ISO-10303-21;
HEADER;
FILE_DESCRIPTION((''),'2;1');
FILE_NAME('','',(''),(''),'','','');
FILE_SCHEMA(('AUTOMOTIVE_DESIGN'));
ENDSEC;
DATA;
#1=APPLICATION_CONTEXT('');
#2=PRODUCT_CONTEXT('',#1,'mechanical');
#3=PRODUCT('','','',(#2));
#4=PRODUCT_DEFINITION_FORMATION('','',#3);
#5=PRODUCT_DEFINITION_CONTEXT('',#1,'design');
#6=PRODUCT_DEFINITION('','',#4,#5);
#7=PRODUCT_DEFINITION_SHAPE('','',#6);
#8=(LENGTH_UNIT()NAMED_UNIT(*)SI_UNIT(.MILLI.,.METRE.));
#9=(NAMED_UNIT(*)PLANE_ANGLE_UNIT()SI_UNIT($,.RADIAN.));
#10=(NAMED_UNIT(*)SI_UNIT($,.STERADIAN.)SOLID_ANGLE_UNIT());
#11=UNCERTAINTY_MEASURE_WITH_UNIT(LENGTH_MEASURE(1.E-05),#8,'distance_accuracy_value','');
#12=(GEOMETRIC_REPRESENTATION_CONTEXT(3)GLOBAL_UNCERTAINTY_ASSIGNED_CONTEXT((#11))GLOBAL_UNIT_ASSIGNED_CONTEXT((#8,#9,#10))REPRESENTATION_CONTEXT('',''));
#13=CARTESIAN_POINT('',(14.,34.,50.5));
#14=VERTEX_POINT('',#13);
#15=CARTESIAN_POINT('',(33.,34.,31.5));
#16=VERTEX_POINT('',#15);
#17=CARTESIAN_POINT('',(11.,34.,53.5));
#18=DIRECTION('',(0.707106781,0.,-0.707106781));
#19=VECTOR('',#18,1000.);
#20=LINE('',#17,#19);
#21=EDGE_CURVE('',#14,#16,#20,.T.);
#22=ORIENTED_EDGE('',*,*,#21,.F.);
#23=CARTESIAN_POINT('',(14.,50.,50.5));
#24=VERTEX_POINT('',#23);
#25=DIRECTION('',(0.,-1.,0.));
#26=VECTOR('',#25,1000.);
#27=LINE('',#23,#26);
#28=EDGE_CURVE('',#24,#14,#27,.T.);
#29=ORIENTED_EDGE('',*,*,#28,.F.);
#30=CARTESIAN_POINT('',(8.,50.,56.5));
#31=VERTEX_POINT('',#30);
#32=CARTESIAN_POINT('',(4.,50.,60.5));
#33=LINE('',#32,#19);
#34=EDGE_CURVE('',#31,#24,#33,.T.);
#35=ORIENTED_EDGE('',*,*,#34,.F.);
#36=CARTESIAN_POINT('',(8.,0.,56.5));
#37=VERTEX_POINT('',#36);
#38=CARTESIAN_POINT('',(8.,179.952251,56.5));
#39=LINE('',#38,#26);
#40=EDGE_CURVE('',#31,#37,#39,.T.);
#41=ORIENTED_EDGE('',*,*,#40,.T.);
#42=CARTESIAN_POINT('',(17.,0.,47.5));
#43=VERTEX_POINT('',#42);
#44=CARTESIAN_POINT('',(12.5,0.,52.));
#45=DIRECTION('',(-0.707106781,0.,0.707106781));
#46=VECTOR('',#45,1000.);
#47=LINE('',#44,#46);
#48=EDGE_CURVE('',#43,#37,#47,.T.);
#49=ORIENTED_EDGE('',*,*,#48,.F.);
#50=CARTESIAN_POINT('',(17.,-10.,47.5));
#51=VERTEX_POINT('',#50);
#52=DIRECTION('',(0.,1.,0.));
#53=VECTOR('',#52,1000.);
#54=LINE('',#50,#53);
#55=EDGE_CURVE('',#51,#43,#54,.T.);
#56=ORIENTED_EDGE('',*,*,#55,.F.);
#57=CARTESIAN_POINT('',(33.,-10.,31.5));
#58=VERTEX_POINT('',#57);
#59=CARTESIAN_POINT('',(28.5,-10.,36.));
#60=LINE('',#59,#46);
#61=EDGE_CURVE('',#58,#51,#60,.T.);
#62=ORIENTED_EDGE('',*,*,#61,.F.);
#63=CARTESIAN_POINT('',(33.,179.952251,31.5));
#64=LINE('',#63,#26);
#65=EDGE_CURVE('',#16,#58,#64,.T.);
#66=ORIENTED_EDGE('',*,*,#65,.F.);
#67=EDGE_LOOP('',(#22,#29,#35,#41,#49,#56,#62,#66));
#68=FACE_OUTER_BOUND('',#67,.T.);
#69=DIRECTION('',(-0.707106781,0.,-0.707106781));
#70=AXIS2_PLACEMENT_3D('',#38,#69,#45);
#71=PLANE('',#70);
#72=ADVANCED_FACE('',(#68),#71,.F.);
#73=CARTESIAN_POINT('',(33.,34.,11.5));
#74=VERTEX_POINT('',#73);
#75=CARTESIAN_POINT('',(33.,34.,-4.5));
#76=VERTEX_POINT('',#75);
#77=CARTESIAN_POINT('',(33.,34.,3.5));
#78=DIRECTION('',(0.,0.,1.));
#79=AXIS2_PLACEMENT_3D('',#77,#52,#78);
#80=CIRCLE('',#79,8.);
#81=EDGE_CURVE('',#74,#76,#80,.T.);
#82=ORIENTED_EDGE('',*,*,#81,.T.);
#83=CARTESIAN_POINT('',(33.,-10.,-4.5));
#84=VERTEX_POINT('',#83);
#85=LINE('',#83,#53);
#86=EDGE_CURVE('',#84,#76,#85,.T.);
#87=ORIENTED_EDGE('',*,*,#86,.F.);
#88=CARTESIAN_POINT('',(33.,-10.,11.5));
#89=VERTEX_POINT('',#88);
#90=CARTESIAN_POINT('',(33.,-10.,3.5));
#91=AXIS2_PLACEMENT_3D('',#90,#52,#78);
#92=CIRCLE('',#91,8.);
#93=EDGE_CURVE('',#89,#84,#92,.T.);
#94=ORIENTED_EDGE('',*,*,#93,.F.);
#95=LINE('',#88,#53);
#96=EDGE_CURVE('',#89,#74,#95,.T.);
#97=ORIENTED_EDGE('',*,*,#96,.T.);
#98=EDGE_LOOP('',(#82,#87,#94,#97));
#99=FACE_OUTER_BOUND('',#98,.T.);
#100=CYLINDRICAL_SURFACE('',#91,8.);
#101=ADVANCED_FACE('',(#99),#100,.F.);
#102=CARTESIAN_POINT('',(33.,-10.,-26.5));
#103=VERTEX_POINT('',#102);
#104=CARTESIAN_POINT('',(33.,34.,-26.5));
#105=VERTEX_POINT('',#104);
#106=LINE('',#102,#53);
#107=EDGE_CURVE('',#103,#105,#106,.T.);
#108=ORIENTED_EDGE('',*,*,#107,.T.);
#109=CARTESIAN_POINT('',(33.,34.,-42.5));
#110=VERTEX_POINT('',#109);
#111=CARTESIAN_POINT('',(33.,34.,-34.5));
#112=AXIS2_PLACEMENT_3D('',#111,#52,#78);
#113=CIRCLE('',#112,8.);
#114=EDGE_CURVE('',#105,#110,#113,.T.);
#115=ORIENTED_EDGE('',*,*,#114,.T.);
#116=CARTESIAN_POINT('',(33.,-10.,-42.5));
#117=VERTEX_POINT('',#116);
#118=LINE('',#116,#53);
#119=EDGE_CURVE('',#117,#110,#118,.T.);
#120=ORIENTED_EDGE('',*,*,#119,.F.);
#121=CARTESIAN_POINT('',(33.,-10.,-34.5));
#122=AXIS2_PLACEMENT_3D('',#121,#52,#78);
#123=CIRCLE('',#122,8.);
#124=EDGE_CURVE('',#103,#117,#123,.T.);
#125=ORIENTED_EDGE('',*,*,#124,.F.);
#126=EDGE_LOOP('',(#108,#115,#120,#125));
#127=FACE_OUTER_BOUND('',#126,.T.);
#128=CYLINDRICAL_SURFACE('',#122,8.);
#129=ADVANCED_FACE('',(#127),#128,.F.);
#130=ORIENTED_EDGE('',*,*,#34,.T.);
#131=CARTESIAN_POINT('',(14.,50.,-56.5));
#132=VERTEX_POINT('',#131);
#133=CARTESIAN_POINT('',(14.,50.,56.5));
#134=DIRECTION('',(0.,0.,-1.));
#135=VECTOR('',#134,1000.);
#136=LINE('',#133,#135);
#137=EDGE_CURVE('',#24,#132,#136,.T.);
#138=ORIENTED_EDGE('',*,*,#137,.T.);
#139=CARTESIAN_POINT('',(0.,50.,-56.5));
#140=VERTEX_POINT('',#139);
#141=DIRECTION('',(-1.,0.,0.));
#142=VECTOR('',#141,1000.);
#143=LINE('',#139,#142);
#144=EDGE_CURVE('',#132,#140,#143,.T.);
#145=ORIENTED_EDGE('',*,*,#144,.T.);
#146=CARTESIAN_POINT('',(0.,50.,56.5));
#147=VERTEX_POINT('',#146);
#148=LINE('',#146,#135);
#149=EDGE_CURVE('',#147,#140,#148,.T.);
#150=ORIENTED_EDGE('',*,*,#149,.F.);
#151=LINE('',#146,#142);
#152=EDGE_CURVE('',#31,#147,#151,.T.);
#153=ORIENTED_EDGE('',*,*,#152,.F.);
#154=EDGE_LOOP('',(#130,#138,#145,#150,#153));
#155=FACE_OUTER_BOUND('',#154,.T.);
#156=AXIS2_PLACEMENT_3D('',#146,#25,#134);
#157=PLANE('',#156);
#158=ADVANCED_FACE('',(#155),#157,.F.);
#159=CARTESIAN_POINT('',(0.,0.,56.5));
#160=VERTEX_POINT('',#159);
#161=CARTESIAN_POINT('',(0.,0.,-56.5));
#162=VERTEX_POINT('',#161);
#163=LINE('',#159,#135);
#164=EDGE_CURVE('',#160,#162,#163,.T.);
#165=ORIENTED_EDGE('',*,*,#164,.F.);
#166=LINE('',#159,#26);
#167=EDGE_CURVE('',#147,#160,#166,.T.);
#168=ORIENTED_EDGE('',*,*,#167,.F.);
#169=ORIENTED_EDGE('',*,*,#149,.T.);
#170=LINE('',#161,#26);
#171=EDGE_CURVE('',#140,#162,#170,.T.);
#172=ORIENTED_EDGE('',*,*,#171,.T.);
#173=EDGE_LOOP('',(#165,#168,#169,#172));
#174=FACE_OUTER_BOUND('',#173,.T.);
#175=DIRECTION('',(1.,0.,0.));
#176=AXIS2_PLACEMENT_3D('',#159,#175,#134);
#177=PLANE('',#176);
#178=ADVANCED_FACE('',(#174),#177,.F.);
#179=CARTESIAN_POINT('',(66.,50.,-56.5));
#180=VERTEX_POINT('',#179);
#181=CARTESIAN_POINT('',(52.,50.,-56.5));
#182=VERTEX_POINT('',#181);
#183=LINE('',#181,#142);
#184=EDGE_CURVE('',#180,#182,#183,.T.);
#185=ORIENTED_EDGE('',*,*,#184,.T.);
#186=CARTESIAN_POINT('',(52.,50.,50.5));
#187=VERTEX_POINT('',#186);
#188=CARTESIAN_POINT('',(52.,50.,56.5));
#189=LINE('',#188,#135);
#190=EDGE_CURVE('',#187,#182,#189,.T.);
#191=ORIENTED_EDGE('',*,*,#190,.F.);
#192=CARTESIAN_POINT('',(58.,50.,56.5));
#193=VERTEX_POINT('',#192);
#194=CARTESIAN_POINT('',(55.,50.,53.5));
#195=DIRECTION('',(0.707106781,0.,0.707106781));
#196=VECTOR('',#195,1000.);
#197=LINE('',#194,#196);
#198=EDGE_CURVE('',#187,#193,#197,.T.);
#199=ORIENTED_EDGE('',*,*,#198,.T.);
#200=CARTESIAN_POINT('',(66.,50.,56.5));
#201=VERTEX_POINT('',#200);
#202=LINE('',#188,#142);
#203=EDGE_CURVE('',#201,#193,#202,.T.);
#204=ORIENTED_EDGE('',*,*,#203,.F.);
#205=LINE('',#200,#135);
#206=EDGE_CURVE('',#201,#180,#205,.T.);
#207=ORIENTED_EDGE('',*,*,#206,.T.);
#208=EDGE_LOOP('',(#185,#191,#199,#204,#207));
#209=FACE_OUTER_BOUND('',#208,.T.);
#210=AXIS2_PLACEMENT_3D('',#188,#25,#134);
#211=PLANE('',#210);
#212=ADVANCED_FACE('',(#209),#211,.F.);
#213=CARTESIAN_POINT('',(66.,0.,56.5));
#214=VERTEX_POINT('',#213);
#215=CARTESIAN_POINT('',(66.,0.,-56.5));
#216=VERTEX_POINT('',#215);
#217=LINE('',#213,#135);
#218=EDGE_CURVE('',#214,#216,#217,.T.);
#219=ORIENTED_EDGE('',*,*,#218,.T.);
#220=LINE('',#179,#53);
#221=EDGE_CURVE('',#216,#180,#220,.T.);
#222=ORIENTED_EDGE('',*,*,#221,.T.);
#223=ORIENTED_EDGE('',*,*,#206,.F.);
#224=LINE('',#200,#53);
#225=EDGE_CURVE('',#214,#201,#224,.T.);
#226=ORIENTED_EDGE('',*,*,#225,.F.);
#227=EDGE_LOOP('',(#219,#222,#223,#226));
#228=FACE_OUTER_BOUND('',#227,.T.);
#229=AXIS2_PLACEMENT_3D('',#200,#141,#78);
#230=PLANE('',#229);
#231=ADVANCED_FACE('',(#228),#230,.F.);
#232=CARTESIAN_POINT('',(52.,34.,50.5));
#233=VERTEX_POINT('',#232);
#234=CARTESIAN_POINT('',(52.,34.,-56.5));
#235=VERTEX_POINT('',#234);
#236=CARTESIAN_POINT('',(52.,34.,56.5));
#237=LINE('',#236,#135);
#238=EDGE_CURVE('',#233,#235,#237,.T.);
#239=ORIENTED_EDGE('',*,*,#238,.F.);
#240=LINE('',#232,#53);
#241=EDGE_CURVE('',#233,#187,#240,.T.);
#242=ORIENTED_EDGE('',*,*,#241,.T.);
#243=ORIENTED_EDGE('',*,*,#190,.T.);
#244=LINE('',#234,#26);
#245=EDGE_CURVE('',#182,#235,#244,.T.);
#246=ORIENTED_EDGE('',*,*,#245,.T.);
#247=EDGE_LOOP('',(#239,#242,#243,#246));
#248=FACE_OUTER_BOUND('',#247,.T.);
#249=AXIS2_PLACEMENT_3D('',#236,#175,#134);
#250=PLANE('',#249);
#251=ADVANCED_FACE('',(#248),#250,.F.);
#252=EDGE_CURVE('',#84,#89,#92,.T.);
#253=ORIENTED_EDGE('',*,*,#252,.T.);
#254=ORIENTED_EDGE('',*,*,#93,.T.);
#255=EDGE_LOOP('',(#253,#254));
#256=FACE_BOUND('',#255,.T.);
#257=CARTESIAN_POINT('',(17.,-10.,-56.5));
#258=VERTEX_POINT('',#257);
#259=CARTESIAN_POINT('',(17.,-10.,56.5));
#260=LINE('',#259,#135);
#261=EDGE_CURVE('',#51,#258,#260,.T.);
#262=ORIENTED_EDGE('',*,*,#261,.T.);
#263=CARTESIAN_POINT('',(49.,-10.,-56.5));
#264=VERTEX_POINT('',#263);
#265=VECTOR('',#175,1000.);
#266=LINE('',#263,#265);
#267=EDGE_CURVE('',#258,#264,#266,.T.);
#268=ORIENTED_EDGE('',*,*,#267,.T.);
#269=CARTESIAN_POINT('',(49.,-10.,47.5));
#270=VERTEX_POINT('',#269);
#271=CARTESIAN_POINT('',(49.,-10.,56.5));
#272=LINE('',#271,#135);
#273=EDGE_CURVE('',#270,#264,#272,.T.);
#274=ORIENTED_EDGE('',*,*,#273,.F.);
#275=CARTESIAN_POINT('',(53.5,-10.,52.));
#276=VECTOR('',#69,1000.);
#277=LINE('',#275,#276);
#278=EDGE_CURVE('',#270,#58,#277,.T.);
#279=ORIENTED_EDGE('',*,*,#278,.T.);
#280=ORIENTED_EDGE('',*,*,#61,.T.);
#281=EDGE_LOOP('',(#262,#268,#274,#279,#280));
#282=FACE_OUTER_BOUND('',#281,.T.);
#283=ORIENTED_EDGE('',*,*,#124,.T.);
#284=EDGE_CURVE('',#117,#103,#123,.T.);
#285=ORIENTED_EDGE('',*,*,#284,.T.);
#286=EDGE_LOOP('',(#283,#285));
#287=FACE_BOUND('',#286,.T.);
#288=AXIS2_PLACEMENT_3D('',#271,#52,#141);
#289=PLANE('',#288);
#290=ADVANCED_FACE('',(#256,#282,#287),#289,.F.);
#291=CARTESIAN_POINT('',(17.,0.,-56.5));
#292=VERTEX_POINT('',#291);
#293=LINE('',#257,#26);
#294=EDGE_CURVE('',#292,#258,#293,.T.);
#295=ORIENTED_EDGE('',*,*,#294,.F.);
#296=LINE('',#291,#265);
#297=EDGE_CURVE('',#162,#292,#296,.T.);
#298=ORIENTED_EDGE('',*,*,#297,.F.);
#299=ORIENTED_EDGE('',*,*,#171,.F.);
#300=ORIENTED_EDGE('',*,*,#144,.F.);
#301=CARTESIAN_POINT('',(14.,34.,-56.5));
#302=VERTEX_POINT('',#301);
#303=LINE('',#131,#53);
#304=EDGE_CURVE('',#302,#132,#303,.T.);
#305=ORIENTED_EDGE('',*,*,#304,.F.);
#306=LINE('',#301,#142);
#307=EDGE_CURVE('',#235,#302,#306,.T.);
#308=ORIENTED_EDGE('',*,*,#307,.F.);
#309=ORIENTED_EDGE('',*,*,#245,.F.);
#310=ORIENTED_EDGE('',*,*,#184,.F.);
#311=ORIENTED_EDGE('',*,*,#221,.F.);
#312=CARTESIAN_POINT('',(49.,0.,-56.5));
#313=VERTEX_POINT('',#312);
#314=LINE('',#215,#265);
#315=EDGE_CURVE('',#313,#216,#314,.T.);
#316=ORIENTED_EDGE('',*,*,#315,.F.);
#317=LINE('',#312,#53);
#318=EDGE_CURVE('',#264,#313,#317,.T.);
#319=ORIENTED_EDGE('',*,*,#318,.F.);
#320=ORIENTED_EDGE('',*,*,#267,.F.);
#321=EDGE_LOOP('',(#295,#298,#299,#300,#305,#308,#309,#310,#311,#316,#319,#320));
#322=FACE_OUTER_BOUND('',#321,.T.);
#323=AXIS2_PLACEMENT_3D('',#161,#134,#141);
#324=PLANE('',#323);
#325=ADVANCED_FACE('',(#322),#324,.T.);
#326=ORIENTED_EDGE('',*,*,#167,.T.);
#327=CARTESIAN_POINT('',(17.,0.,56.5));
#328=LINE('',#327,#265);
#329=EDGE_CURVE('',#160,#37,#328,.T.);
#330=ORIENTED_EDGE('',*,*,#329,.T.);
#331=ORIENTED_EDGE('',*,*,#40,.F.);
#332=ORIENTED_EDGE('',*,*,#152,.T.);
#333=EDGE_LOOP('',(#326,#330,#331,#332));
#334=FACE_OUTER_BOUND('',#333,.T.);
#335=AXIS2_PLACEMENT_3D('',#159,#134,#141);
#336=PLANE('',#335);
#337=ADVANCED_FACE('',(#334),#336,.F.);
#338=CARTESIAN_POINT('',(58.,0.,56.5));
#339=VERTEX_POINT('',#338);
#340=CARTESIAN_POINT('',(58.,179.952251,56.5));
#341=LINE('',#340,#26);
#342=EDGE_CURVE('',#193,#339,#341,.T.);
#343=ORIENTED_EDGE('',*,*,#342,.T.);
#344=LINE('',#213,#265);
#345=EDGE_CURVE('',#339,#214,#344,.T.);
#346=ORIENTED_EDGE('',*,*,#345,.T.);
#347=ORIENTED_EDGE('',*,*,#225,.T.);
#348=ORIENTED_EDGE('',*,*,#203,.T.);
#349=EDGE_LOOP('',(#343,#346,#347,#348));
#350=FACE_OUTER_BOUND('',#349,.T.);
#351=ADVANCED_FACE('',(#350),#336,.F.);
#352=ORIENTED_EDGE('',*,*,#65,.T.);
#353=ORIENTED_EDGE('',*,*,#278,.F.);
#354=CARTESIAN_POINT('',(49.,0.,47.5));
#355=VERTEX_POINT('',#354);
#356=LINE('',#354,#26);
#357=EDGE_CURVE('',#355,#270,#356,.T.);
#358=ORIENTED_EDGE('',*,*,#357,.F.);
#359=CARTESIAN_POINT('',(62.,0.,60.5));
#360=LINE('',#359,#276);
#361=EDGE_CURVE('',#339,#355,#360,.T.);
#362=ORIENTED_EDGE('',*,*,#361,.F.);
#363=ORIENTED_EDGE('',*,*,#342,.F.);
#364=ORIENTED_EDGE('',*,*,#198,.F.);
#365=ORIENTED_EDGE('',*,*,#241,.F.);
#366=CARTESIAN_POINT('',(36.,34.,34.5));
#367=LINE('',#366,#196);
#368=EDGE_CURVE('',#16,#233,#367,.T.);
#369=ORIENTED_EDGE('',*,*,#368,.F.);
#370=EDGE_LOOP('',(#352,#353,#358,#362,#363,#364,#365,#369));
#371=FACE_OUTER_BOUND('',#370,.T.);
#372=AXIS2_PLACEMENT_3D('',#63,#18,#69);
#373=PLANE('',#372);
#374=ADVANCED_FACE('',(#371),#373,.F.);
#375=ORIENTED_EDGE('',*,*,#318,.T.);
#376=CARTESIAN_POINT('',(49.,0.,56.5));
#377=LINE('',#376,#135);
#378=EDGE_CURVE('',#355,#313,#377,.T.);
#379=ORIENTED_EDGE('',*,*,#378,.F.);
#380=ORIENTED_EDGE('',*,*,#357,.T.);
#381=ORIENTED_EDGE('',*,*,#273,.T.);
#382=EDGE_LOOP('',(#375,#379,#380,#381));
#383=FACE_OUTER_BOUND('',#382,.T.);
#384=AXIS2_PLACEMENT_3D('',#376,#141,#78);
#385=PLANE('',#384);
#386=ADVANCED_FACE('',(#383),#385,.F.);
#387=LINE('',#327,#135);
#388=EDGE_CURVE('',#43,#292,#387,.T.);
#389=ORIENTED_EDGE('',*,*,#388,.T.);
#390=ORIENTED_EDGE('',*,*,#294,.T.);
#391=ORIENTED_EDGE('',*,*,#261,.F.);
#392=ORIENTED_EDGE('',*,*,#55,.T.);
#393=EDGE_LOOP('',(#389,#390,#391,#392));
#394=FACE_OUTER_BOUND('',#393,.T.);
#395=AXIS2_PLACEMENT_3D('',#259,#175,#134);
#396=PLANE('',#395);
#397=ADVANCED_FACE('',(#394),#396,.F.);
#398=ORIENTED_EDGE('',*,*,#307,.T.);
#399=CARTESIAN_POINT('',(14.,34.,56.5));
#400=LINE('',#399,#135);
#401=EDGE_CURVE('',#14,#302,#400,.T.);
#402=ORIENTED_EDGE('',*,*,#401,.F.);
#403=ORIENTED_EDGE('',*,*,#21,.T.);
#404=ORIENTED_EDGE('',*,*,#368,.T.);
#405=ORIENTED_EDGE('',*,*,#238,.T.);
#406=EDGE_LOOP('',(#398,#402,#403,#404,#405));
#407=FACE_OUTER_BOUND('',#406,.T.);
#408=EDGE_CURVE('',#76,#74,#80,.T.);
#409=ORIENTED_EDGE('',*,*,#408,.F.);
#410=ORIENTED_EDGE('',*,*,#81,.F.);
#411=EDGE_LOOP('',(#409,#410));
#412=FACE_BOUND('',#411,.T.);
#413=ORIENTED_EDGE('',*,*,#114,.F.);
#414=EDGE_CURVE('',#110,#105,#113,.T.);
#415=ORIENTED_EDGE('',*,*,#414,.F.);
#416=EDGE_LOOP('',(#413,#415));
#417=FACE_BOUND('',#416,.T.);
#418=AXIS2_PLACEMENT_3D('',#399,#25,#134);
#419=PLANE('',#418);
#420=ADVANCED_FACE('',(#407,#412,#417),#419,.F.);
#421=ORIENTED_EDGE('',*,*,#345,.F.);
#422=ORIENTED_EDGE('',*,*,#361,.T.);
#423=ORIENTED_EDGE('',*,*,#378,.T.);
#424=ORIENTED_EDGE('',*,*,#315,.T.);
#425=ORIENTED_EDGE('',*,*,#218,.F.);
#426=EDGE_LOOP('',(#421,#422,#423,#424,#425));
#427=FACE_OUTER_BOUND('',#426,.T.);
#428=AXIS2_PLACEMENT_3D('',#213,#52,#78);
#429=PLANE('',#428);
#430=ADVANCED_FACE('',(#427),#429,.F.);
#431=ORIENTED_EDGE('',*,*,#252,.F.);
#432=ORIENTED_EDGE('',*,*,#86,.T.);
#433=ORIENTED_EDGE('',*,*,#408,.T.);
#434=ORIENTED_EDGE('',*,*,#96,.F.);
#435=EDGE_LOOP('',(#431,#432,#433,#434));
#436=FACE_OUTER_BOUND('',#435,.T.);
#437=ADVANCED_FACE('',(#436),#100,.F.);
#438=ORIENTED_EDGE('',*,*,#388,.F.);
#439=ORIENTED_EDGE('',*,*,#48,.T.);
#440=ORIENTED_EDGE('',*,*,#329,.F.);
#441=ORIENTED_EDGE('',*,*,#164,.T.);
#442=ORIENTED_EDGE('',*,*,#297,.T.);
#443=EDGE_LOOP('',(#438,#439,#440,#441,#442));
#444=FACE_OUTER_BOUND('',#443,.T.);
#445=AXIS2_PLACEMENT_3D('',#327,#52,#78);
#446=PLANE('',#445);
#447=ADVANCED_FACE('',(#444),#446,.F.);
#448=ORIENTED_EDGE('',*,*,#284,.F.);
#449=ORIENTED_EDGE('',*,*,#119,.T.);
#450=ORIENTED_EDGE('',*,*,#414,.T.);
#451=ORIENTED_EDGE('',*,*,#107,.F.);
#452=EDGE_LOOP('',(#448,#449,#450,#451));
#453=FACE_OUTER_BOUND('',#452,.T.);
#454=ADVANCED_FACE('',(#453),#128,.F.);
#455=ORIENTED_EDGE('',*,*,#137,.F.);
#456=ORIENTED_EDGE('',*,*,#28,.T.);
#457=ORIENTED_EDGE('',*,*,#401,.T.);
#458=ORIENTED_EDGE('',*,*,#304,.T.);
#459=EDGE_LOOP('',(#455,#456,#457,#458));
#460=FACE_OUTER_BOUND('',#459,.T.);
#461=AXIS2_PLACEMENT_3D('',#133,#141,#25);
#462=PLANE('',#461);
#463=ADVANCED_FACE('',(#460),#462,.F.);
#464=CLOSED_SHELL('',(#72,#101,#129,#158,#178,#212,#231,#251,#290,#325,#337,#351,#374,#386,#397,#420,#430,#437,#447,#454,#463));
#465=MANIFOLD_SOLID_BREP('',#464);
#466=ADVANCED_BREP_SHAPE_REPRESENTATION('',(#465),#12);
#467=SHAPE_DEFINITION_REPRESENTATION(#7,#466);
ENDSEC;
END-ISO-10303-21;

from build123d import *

# Parameters (mm, degrees)
CHANNEL_BLOCK_DEPTH       = 56.5
THROUGH_HOLES_SKETCH_R    = 8
THROUGH_HOLES_2X_16_DEPTH = 98.387114137
SIDE_CUT_DEPTH            = 101.240959692
SIDE_CUT_DEPTH_BACK       = 101.240959692


with BuildPart() as part:
    # Channel Profile Sketch → Channel Block (new, symmetric)
    with BuildSketch(Plane.XY):
        Polygon((0, 0), (0, 50), (14, 50), (14, 34), (52, 34), (52, 50), (66, 50), (66, 0), (49, 0), (49, -10), (17, -10), (17, 0), align=None)
    extrude(amount=CHANNEL_BLOCK_DEPTH, both=True)

    # Through Holes Sketch → Through Holes 2xØ16 (cut, through all)
    with BuildSketch(Plane(origin=(0, 34, 0), x_dir=(1, 0, 0), z_dir=(0, 1, 0))):
        with Locations(Location((33, 34.5, 0), (0, 0, 270))):
            Circle(THROUGH_HOLES_SKETCH_R)
        with Locations(Location((33, -3.5, 0), (0, 0, 270))):
            Circle(THROUGH_HOLES_SKETCH_R)
    extrude(amount=-THROUGH_HOLES_2X_16_DEPTH, mode=Mode.SUBTRACT)

    # Side Cut Sketch → Side Cut (cut, two sides: drawn at the far end of the back side and taken through both)
    with BuildSketch(Plane(origin=(0, 0, 0), x_dir=(1, 0, 0), z_dir=(0, 1, 0)).offset(-SIDE_CUT_DEPTH_BACK)):
        Polygon((-178.698459932, -243.198459932), (8, -56.5), (33, -31.5), (58, -56.5), (244.698459932, -243.198459932), (244.698459932, -771.261448153), (-178.698459932, -771.261448153), align=None)
    extrude(amount=SIDE_CUT_DEPTH + SIDE_CUT_DEPTH_BACK, mode=Mode.SUBTRACT)


solid = part.part
